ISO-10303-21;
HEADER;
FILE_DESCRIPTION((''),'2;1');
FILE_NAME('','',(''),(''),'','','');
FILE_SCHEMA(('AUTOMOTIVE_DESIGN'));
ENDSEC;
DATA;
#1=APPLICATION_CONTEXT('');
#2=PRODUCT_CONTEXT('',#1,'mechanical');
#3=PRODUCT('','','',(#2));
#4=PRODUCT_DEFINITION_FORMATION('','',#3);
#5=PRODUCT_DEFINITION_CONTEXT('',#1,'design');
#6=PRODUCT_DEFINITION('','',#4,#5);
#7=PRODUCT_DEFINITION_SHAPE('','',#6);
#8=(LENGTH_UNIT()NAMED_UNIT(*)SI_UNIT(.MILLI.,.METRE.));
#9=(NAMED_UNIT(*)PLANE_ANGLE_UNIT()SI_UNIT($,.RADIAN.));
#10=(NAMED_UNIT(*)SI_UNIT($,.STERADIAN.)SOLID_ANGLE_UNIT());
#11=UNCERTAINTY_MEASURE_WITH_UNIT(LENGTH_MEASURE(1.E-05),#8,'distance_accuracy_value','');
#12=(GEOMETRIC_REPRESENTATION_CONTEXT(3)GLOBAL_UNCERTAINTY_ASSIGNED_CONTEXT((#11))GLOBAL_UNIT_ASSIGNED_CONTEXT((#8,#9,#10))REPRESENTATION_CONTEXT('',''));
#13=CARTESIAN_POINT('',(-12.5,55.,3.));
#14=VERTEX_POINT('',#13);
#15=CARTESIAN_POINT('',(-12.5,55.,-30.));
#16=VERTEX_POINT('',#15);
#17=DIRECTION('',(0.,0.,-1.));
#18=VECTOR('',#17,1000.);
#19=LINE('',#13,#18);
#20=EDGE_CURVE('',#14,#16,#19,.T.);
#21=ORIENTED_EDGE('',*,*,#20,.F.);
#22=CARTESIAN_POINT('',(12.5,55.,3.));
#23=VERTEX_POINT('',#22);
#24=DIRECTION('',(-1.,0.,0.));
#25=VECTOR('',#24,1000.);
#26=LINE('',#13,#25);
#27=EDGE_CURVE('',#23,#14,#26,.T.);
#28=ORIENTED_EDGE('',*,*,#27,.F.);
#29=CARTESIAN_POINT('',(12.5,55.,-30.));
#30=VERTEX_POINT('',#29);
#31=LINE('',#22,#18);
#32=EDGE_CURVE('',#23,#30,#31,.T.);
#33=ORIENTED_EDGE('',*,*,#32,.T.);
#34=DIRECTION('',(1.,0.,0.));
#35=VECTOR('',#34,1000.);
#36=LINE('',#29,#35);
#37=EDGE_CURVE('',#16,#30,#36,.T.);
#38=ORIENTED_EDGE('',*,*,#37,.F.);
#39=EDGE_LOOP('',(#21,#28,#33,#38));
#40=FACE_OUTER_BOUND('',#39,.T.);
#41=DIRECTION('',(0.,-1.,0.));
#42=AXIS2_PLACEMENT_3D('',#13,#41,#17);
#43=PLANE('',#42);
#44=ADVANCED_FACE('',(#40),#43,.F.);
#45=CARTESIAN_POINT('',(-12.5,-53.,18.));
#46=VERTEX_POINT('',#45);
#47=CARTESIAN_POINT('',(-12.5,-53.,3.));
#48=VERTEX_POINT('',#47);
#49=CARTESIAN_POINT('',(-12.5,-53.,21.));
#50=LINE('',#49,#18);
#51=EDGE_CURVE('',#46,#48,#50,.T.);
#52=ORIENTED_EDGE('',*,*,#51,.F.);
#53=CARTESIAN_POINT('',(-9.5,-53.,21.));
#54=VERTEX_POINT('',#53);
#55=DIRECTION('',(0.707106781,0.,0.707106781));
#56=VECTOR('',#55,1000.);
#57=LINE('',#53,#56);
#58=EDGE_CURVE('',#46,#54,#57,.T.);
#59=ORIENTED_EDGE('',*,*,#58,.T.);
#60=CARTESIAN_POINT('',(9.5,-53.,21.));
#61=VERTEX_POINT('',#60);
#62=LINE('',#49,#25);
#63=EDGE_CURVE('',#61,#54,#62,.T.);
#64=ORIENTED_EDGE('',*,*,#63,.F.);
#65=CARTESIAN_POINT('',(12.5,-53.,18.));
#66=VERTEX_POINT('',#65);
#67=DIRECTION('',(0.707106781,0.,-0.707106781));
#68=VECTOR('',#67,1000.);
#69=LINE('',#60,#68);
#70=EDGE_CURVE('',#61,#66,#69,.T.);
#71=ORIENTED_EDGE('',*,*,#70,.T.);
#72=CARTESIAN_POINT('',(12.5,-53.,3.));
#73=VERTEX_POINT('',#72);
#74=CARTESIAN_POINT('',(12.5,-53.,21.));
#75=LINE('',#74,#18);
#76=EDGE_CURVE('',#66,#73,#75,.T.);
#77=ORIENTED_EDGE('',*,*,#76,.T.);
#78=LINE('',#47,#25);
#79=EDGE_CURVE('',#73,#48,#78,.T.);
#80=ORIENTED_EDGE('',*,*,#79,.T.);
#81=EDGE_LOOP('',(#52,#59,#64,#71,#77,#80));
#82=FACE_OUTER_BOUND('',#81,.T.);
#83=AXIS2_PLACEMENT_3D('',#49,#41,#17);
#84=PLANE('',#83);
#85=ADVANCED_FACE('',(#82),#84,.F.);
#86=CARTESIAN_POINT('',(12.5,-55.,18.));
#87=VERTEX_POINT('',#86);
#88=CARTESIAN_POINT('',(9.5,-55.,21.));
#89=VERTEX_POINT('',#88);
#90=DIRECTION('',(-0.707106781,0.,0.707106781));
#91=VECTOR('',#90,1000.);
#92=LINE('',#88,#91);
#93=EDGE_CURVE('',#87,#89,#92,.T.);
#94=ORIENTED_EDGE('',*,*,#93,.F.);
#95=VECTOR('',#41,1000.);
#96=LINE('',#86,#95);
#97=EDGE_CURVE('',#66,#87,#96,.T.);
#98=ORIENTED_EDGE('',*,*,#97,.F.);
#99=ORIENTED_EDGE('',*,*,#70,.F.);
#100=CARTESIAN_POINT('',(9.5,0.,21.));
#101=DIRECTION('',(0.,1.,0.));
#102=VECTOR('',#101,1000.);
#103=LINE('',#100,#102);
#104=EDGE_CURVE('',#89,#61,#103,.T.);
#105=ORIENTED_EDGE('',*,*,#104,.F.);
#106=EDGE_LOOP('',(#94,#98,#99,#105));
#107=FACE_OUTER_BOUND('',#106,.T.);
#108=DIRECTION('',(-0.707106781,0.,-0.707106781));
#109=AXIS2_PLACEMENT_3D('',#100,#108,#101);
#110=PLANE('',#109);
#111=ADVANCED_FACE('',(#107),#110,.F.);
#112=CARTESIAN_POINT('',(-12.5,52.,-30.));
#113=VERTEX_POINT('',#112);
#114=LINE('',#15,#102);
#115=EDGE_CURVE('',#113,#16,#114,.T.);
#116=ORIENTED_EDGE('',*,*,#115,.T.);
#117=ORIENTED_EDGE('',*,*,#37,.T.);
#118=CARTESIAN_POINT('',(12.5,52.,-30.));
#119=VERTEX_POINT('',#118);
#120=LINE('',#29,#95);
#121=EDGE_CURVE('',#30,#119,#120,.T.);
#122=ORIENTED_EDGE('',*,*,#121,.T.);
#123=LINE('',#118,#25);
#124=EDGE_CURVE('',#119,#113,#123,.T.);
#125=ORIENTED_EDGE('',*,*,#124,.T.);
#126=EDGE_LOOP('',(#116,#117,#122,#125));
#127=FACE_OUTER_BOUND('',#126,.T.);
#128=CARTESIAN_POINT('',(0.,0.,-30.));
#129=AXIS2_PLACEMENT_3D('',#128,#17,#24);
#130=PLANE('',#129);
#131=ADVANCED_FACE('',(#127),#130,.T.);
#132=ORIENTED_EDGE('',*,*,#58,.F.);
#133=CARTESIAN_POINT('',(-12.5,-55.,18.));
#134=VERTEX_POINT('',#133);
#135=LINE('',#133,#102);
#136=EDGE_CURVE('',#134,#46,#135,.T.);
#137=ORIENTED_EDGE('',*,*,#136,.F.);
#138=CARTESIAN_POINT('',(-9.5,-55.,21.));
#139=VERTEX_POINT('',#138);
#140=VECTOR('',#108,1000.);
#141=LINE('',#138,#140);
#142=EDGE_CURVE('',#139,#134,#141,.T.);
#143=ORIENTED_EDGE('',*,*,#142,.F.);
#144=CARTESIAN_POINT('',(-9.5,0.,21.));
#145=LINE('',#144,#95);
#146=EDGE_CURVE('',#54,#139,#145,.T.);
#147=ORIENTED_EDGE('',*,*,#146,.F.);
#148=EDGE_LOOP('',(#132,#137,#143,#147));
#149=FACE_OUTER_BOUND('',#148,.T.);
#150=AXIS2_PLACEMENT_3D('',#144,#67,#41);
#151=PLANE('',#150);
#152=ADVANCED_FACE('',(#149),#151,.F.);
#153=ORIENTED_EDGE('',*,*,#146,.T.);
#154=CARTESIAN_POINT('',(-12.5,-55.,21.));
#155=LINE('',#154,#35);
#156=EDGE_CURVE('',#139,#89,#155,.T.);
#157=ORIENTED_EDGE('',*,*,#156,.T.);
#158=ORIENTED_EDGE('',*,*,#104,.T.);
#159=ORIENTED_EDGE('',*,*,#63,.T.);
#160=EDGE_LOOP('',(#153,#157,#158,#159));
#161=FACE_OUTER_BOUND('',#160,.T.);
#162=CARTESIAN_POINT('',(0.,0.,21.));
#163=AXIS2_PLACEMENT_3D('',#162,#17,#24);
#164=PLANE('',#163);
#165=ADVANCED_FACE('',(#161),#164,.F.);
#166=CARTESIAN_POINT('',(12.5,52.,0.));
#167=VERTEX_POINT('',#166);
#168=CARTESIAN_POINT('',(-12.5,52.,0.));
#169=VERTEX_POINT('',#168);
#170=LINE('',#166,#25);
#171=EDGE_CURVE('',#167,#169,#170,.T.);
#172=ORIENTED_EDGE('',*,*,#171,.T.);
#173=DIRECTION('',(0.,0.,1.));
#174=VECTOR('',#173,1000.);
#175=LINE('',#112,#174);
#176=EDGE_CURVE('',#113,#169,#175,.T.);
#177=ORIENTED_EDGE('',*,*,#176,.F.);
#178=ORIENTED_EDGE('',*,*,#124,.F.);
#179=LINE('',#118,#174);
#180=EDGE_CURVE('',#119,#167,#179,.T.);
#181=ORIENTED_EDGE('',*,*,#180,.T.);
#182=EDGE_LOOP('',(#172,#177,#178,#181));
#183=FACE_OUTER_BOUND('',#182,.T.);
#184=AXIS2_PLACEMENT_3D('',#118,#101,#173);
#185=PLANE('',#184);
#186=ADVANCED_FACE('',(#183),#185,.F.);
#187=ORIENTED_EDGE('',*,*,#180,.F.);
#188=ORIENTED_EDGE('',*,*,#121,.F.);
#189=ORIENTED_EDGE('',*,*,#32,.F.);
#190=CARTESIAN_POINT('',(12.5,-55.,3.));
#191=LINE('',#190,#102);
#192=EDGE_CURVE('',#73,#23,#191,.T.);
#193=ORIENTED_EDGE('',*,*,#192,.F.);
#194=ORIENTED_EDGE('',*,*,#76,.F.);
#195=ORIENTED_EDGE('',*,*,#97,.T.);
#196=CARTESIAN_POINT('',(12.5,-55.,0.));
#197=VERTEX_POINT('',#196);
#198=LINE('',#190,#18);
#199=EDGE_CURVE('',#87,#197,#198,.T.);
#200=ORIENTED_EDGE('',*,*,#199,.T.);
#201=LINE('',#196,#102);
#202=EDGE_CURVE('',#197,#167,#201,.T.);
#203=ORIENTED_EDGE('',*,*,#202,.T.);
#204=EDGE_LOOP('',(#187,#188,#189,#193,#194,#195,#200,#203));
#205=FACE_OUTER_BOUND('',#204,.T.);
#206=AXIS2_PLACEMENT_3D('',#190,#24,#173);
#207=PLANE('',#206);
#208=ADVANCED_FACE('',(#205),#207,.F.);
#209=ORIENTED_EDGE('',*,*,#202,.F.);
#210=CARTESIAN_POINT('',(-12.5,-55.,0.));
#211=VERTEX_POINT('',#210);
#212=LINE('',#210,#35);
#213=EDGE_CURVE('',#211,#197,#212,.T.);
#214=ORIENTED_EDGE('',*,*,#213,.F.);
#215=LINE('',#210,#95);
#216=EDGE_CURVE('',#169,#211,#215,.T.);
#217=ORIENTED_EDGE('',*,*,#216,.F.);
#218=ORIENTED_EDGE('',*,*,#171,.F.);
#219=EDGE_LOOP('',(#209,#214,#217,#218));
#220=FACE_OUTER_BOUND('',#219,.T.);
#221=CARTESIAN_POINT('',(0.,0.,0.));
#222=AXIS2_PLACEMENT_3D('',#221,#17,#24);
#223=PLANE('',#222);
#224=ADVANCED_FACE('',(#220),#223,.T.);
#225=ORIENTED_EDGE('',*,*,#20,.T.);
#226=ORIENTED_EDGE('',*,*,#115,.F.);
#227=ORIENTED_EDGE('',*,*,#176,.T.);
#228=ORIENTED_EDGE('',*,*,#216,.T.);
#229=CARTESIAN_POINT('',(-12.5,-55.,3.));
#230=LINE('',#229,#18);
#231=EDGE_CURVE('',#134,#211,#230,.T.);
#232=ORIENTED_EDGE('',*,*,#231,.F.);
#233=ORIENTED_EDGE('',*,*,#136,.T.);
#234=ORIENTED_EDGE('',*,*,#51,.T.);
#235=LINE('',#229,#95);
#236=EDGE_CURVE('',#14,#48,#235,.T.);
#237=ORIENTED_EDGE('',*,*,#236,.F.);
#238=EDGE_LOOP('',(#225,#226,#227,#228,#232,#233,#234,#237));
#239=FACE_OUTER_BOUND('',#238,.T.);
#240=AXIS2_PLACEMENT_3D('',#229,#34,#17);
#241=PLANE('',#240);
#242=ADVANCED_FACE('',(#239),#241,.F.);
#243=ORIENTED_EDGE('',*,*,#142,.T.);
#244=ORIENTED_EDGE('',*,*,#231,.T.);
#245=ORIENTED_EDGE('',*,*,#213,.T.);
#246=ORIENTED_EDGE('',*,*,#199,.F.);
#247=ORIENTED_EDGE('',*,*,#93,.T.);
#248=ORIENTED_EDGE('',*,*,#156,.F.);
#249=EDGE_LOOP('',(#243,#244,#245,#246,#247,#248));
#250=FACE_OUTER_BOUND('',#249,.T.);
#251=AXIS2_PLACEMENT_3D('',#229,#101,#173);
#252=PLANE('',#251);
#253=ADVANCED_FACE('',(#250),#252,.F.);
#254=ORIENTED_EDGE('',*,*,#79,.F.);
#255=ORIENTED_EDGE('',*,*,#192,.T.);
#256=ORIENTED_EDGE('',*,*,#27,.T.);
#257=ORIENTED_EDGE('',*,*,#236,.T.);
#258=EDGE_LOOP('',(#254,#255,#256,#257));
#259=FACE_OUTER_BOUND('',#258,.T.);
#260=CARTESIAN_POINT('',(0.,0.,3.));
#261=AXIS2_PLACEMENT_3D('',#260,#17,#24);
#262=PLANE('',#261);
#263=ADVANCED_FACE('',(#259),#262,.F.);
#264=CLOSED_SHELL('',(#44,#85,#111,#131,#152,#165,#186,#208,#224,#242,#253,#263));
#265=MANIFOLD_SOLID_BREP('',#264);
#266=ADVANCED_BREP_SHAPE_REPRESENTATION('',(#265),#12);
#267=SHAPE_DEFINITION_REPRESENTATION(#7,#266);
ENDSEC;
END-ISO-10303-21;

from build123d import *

# Parameters (mm, degrees)
SKETCH_1_W      = 25
SKETCH_1_H      = 110
EXTRUDE_1_DEPTH = 3
SKETCH_3_W      = 25
SKETCH_3_H      = 2
EXTRUDE_2_DEPTH = 18
SKETCH_4_W      = 25
SKETCH_4_H      = 3
EXTRUDE_3_DEPTH = 30
CHAMFER_1_SIZE  = 3


with BuildPart() as part:
    # 草图1 → 凸台-拉伸1 (new body)
    with BuildSketch(Plane.XY):
        Rectangle(SKETCH_1_W, SKETCH_1_H)
    extrude(amount=EXTRUDE_1_DEPTH)

    # 草图3 → 凸台-拉伸2 (add)
    with BuildSketch(Plane.XY.offset(3)):
        with Locations((0, -54)):
            Rectangle(SKETCH_3_W, SKETCH_3_H)
    extrude(amount=EXTRUDE_2_DEPTH)

    # 草图4 → 凸台-拉伸3 (add)
    with BuildSketch(Plane(origin=(0, 0, 0), x_dir=(-1, 0, 0), z_dir=(0, 0, -1))):
        with Locations((0, 53.5)):
            Rectangle(SKETCH_4_W, SKETCH_4_H)
    extrude(amount=EXTRUDE_3_DEPTH)

    # 倒角1
    chamfer_1_edges = [part.edges().sort_by_distance(p)[0] for p in [
        (-12.5, -54, 21),
        (12.5, -54, 21),
    ]]
    chamfer(chamfer_1_edges, length=CHAMFER_1_SIZE)


solid = part.part
